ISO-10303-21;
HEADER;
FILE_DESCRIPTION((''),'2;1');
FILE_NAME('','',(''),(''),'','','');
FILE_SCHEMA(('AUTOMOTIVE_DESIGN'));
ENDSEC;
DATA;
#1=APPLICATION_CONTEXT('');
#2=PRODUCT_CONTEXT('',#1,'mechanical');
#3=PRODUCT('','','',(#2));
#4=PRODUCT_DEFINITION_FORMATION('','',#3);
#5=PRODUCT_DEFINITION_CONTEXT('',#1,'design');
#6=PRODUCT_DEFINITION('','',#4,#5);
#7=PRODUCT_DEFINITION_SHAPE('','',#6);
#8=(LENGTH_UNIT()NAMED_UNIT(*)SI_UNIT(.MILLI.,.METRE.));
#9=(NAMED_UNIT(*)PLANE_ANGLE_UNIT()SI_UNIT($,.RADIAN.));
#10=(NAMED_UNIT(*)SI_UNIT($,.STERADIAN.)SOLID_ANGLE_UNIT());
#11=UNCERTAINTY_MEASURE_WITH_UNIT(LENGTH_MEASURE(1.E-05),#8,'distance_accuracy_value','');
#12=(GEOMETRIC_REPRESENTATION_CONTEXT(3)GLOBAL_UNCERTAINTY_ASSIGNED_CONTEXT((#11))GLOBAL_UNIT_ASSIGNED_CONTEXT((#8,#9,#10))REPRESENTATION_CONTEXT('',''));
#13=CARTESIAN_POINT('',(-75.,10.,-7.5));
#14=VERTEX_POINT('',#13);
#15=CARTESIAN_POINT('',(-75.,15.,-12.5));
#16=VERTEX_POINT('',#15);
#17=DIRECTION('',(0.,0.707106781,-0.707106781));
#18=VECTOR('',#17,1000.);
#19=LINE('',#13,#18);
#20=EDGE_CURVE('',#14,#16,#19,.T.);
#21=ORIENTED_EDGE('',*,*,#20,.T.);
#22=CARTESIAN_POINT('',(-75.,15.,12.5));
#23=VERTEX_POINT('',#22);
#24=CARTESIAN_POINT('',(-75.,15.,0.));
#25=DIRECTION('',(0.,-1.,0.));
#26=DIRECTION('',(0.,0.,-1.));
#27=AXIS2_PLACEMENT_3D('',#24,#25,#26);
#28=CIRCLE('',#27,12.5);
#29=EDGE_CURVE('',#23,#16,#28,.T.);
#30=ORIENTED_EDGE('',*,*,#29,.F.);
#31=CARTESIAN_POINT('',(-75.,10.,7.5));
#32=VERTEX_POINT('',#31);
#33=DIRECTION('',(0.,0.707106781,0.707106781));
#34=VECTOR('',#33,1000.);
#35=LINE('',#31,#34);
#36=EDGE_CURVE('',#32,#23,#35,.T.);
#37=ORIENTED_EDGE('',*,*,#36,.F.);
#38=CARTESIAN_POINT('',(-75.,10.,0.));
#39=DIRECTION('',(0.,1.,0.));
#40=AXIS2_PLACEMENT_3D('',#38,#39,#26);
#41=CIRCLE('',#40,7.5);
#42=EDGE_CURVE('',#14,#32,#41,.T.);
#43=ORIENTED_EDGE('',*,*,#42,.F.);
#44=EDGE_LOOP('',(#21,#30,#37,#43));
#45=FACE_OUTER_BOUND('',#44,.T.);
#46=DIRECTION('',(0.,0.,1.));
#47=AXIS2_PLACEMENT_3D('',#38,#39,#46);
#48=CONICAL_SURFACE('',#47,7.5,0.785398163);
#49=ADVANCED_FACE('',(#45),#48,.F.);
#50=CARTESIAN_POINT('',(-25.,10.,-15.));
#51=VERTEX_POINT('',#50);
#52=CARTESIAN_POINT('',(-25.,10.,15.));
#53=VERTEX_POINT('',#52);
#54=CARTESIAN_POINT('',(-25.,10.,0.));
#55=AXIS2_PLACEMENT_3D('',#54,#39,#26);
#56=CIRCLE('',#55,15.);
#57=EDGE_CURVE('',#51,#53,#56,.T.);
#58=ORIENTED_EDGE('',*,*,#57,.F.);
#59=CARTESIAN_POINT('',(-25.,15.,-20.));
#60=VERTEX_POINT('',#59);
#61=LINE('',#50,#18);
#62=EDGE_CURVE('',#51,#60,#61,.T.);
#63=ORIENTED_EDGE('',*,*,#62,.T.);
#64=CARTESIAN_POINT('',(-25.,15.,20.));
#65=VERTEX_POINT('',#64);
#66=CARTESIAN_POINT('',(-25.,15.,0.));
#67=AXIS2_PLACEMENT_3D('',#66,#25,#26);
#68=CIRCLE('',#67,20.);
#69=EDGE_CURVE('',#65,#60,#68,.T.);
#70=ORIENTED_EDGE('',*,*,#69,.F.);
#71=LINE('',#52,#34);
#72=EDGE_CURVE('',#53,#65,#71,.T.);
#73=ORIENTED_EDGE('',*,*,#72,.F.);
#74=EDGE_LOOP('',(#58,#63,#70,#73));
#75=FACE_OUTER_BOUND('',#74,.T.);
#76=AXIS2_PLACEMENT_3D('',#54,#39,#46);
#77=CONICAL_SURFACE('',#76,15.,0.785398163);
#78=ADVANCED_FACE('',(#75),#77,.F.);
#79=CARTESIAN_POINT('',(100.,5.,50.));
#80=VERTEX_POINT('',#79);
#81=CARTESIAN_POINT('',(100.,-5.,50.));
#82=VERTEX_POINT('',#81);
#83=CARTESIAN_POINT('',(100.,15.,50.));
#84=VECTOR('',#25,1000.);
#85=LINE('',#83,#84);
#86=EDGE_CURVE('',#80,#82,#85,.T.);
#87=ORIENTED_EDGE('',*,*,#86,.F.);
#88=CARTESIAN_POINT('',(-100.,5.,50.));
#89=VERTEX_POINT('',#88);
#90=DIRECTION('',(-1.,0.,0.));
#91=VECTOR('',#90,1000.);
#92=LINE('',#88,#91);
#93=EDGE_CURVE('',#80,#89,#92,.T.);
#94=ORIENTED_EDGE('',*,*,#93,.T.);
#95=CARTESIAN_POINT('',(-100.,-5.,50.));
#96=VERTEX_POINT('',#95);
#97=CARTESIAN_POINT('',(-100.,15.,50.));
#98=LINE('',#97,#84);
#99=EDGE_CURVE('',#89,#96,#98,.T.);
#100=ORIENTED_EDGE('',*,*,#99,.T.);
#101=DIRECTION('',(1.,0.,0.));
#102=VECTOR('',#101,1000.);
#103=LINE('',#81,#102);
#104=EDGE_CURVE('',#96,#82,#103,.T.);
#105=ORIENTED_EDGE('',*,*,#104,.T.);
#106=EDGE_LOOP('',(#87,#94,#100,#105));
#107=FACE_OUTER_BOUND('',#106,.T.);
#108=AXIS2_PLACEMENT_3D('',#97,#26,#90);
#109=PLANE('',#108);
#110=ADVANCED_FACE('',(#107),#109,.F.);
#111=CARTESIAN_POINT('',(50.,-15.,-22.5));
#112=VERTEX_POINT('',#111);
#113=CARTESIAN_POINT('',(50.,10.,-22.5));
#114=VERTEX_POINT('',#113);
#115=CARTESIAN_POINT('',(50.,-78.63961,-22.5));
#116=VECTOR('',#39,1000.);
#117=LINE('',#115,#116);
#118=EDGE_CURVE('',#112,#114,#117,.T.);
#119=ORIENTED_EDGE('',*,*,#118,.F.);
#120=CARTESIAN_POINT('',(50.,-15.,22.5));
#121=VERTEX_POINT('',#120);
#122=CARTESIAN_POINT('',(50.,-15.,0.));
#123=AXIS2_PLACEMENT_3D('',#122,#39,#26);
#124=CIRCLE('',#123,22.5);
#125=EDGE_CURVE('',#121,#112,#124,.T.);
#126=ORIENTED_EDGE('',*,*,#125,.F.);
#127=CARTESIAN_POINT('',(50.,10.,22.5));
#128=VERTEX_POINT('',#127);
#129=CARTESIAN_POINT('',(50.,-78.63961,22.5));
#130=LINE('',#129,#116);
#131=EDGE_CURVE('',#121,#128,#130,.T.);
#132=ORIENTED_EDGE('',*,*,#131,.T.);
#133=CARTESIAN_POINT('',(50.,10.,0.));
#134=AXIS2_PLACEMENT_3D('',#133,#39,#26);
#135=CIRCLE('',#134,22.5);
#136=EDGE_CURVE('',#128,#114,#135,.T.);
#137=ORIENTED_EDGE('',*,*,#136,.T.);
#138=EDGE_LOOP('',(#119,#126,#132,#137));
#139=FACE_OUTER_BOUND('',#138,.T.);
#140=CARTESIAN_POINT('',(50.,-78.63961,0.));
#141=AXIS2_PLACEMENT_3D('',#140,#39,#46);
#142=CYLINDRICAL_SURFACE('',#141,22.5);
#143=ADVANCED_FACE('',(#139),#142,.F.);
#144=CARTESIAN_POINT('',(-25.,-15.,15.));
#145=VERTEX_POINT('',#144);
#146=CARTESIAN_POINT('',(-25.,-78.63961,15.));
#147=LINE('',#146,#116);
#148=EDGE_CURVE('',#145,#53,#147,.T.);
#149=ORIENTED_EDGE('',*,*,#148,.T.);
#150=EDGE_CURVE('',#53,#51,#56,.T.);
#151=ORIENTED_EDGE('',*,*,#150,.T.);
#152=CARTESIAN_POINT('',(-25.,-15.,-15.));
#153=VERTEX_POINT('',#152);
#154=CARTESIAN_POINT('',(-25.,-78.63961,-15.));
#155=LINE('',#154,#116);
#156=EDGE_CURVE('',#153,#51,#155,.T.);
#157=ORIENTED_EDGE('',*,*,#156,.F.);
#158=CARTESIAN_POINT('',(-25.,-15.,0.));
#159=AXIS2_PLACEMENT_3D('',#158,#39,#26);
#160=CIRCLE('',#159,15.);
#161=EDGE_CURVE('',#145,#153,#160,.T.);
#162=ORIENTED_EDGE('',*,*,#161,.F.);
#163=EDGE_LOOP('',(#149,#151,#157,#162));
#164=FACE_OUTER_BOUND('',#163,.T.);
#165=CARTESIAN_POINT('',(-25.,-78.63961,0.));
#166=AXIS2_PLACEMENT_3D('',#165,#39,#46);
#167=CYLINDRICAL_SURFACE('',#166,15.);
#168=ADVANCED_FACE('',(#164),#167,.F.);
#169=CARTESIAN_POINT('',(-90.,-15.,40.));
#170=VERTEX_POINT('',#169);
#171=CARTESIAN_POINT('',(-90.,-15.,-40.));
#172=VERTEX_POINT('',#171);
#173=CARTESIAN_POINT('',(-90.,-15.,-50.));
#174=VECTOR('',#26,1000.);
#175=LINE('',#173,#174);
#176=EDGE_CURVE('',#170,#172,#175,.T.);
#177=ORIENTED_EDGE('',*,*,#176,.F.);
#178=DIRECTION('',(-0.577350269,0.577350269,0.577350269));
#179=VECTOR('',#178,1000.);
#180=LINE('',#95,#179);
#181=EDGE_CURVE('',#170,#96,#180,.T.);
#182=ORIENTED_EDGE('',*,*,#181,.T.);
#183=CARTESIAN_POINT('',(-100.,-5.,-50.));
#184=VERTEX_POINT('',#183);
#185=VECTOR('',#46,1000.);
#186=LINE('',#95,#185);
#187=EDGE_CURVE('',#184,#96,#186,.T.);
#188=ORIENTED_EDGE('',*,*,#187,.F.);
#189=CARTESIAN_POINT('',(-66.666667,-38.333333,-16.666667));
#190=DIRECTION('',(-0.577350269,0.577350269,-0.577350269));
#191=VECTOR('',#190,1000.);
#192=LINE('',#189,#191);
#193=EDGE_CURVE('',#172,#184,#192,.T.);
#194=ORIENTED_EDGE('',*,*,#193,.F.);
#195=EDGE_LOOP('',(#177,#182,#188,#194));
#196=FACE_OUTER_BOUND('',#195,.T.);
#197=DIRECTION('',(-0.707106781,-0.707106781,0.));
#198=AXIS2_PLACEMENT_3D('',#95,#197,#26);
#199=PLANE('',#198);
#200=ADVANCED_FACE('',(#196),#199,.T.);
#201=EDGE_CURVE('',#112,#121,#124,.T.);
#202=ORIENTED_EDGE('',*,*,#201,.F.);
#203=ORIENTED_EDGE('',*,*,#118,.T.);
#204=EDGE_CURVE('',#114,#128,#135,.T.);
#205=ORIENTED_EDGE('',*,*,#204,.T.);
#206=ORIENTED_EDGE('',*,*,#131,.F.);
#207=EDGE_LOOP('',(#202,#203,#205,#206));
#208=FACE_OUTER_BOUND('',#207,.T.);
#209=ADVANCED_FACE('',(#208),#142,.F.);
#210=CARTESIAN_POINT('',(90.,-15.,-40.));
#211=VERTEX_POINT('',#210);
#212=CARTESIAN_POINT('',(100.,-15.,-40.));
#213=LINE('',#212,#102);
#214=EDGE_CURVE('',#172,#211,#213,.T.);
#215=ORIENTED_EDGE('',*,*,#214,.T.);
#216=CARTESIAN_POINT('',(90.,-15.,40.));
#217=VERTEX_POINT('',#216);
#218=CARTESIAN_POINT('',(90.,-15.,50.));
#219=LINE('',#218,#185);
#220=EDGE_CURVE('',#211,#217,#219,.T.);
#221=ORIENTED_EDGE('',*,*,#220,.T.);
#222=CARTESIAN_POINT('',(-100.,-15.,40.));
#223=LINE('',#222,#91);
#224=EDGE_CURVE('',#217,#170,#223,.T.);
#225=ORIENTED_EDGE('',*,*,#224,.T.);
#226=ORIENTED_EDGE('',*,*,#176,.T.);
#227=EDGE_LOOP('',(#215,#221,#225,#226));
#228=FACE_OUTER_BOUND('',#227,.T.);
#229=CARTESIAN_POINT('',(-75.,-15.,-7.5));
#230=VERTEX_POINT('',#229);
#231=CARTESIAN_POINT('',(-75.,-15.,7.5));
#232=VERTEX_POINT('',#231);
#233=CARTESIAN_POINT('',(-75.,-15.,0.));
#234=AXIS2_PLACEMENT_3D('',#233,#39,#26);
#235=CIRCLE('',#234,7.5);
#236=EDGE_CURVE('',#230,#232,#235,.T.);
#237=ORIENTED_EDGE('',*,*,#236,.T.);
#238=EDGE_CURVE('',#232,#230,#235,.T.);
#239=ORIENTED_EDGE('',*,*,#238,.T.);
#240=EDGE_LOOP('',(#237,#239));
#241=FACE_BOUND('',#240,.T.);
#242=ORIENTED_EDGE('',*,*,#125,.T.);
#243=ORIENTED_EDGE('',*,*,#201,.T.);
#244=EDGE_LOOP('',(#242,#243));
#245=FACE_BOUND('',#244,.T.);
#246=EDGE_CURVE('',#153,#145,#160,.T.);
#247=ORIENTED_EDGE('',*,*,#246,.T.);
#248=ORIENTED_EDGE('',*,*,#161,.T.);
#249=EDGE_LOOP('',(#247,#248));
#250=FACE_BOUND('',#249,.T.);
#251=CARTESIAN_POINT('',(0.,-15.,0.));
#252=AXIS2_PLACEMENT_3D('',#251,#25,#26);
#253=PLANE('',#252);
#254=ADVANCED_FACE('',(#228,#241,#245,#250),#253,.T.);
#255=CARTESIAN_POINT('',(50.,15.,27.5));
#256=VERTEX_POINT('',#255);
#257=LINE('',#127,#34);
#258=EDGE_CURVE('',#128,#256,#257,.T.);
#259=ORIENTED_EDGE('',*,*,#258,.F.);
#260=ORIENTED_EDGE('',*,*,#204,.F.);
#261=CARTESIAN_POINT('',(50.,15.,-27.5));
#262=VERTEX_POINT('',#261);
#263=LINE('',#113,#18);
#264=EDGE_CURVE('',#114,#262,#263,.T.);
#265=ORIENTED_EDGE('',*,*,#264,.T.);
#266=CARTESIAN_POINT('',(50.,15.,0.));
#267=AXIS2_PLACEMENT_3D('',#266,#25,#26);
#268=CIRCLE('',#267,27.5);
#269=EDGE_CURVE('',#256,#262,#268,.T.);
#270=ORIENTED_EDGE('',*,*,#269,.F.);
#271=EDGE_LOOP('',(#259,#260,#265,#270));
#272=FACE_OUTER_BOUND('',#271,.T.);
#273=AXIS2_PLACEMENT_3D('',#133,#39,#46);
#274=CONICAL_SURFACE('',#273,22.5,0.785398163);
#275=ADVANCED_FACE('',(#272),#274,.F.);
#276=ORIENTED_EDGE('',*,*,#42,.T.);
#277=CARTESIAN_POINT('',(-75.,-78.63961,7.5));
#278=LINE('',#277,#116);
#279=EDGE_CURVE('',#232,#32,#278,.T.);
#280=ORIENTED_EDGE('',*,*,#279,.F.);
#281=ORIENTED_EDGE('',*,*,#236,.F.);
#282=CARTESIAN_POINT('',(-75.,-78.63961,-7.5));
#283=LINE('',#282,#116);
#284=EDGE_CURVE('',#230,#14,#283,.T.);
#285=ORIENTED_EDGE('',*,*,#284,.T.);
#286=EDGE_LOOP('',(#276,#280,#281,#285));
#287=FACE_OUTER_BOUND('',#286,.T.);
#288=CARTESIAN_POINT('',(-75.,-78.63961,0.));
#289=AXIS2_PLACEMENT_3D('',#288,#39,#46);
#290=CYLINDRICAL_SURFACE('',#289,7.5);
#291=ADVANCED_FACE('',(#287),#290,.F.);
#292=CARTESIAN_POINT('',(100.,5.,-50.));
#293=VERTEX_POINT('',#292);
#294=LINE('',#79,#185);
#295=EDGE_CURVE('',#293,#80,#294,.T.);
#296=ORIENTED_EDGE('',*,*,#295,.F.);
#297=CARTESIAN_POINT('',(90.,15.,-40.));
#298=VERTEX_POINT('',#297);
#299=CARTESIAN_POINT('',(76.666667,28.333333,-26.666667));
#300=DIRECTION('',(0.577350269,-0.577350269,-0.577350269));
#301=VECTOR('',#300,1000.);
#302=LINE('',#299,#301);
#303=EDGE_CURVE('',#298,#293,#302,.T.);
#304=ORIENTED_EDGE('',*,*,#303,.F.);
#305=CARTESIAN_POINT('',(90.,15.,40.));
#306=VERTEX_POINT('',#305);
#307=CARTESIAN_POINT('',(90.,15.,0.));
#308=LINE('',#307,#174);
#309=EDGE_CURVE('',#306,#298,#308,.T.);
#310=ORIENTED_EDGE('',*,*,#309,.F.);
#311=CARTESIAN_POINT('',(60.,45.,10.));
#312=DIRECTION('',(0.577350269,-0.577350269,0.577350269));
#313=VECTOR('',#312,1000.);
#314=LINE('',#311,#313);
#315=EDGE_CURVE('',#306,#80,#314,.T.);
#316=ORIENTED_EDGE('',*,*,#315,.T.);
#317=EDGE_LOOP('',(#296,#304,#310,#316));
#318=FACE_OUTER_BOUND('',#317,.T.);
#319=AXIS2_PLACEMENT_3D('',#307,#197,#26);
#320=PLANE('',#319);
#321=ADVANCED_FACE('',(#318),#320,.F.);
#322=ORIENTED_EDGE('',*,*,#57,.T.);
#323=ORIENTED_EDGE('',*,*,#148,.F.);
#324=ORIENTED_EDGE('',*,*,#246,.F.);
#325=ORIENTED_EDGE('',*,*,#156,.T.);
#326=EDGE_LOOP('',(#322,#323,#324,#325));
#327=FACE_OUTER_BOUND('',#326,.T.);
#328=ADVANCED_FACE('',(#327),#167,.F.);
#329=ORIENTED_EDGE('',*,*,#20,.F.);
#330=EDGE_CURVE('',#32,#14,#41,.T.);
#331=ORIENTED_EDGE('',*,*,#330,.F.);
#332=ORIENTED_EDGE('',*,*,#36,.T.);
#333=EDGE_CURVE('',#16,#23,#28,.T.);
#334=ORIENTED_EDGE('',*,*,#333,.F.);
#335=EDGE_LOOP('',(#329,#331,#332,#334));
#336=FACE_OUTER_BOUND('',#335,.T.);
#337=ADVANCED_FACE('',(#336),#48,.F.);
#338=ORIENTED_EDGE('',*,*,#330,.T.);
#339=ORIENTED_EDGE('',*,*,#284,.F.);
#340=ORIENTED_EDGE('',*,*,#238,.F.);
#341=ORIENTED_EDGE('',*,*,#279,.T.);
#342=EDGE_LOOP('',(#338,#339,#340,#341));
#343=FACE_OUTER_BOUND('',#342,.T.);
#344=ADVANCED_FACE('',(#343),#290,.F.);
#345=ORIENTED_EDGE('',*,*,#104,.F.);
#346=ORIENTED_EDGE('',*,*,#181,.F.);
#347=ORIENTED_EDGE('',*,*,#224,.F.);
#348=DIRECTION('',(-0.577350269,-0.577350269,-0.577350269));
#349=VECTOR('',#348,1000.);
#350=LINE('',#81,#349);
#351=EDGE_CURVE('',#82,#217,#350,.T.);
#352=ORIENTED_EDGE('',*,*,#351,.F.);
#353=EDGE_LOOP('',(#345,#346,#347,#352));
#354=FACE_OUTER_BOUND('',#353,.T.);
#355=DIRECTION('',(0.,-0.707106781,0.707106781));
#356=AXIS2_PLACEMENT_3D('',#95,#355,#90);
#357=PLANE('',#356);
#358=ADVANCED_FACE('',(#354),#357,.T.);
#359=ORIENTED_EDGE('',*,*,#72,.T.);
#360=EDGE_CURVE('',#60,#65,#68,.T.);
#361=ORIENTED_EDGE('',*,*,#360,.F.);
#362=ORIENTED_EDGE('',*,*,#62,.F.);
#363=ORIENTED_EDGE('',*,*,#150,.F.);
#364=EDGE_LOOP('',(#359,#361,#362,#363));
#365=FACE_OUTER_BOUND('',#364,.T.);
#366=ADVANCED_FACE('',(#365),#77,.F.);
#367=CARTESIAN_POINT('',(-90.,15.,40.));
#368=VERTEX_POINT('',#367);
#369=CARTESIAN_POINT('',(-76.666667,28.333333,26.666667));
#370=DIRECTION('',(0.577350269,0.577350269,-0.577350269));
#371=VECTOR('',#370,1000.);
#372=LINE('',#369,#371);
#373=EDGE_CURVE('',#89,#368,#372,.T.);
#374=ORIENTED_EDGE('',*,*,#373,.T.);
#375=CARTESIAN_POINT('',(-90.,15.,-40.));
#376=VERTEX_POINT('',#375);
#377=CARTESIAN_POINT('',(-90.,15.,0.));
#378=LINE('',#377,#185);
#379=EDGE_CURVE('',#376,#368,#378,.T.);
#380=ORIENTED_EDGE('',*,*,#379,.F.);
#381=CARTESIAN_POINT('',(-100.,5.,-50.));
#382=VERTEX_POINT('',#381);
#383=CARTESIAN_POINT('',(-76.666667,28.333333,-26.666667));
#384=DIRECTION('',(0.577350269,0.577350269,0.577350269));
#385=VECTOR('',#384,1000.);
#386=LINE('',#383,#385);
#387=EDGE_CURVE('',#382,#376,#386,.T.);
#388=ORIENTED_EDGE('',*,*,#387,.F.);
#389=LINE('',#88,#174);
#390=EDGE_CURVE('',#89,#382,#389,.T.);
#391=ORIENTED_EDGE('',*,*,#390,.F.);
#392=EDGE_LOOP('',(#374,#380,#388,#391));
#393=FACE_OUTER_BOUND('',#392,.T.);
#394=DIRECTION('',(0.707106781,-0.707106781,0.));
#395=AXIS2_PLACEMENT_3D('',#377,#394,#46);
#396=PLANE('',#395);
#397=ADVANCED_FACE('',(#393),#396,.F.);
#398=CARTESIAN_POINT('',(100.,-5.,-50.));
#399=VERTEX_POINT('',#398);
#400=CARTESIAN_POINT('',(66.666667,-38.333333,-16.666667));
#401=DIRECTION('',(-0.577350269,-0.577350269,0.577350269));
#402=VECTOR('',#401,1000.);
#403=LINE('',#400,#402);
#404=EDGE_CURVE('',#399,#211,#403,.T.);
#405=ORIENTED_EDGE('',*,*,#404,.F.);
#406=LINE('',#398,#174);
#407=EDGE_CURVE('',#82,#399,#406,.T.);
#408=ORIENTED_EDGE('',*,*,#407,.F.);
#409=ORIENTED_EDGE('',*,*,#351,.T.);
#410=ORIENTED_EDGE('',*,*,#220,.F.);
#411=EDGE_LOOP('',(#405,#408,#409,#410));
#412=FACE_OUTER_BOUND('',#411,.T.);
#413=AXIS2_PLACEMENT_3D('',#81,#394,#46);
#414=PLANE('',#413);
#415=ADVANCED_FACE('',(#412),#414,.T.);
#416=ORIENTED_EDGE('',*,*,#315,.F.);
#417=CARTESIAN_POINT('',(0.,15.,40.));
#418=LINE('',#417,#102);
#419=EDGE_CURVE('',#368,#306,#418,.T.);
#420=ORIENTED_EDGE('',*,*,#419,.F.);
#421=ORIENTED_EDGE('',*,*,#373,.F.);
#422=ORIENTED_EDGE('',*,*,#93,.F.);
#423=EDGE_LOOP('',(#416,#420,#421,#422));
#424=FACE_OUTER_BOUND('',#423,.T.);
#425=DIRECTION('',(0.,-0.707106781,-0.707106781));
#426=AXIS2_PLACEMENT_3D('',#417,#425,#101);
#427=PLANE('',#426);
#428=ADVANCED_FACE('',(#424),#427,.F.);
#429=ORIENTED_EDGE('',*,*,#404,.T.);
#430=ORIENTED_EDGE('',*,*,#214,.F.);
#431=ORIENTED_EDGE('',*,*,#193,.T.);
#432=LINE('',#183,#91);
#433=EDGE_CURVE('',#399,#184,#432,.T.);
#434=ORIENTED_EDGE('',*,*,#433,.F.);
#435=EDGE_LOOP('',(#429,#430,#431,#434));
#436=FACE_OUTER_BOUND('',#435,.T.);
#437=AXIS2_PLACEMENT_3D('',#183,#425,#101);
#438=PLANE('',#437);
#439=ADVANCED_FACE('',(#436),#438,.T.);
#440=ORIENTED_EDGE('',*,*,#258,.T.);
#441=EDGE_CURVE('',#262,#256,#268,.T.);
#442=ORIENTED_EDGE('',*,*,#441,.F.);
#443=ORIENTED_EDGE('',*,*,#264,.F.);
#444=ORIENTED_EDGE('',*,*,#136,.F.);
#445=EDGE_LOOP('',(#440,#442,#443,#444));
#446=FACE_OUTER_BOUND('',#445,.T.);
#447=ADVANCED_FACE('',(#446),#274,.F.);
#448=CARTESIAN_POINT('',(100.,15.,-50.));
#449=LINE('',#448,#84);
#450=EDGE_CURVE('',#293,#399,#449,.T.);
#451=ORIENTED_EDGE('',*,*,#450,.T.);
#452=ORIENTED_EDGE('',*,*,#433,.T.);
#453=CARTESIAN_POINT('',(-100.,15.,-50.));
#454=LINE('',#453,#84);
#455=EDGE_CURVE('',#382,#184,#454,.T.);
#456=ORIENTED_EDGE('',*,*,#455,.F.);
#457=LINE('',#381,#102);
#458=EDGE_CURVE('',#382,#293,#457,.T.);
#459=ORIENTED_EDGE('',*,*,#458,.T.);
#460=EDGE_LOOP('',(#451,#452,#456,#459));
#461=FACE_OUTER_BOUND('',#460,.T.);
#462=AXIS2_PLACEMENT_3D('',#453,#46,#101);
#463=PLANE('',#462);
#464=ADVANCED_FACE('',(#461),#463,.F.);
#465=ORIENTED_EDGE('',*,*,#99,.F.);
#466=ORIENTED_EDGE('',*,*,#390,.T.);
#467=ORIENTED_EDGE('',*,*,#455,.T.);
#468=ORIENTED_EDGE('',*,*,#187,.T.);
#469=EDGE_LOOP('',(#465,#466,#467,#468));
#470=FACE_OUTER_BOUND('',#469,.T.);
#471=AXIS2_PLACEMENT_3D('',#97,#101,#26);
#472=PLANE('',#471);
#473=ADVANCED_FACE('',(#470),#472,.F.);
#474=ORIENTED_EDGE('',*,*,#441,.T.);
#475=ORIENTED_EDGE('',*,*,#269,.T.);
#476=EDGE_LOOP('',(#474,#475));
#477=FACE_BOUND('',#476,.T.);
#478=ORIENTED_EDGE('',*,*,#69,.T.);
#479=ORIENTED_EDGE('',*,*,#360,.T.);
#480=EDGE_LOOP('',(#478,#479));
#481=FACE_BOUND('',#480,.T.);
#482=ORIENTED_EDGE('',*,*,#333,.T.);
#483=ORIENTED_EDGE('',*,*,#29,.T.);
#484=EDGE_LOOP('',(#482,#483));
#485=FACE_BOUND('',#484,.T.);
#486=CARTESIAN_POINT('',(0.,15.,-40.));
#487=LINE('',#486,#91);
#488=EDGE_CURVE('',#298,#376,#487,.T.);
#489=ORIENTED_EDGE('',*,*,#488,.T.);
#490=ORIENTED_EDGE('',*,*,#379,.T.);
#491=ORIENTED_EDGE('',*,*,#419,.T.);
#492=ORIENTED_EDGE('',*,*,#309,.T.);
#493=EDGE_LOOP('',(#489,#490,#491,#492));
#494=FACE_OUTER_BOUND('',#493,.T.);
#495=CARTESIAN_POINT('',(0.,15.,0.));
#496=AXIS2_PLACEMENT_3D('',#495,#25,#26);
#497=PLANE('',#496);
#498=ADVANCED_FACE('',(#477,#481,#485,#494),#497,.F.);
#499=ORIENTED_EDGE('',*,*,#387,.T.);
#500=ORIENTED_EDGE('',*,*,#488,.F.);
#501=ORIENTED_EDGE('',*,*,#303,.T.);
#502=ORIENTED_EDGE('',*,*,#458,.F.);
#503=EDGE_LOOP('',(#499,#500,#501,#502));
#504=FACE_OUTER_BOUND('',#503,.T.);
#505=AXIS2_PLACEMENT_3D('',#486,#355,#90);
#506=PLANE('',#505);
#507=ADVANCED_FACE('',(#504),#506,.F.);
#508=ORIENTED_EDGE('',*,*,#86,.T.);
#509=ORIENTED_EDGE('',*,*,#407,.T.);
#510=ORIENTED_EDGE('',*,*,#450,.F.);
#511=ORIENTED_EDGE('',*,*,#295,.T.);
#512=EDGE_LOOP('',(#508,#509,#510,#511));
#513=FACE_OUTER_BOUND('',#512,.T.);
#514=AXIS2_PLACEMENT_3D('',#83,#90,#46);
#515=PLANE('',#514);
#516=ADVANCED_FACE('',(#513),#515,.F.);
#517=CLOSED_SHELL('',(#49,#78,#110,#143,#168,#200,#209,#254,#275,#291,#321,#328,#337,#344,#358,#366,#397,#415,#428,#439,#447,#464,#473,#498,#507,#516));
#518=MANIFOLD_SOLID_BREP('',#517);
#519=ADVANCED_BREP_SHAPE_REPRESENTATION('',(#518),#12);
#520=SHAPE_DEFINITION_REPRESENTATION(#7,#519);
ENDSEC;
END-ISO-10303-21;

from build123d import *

# Parameters (mm, degrees)
BASE_PLATE_SKETCH_W          = 200
BASE_PLATE_SKETCH_H          = 100
BASE_PLATE_200X100X30_DEPTH  = 15
PLATE_END_CHAMFERS_10MM_SIZE = 10
PIN_HOLES_SKETCH_R           = 7.5
PIN_HOLES_SKETCH_R_2         = 15
PIN_HOLES_SKETCH_R_3         = 22.5
PIN_HOLES_15_30_45_DEPTH     = 30
PIN_HOLE_CHAMFERS_5MM_SIZE   = 5


with BuildPart() as part:
    # Base Plate Sketch → Base Plate 200x100x30 (new, symmetric)
    with BuildSketch(Plane(origin=(0, 0, 0), x_dir=(1, 0, 0), z_dir=(0, 1, 0))):
        Rectangle(BASE_PLATE_SKETCH_W, BASE_PLATE_SKETCH_H)
    extrude(amount=BASE_PLATE_200X100X30_DEPTH, both=True)

    # Plate End Chamfers 10mm
    plate_end_chamfers_10mm_edges = [part.edges().sort_by_distance(p)[0] for p in [
        (-100, 15, 0),
        (0, 15, 50),
        (100, 15, 0),
        (0, -15, 50),
        (-100, -15, 0),
        (0, -15, -50),
        (100, -15, 0),
        (0, 15, -50),
    ]]
    chamfer(plate_end_chamfers_10mm_edges, length=PLATE_END_CHAMFERS_10MM_SIZE)

    # Pin Holes Sketch → Pin Holes Ø15 Ø30 Ø45 (cut)
    with BuildSketch(Plane(origin=(0, 15, 0), x_dir=(1, 0, 0), z_dir=(0, 1, 0))):
        with Locations(Location((-75, 0, 0), (0, 0, 270))):
            Circle(PIN_HOLES_SKETCH_R)
        with Locations(Location((-25, 0, 0), (0, 0, 270))):
            Circle(PIN_HOLES_SKETCH_R_2)
        with Locations(Location((50, 0, 0), (0, 0, 270))):
            Circle(PIN_HOLES_SKETCH_R_3)
    extrude(amount=-PIN_HOLES_15_30_45_DEPTH, mode=Mode.SUBTRACT)

    # Pin Hole Chamfers 5mm
    pin_hole_chamfers_5mm_edges = [part.edges().sort_by_distance(p)[0] for p in [
        (-75, 15, -7.5),
        (-25, 15, -15),
        (50, 15, -22.5),
    ]]
    chamfer(pin_hole_chamfers_5mm_edges, length=PIN_HOLE_CHAMFERS_5MM_SIZE)


solid = part.part
